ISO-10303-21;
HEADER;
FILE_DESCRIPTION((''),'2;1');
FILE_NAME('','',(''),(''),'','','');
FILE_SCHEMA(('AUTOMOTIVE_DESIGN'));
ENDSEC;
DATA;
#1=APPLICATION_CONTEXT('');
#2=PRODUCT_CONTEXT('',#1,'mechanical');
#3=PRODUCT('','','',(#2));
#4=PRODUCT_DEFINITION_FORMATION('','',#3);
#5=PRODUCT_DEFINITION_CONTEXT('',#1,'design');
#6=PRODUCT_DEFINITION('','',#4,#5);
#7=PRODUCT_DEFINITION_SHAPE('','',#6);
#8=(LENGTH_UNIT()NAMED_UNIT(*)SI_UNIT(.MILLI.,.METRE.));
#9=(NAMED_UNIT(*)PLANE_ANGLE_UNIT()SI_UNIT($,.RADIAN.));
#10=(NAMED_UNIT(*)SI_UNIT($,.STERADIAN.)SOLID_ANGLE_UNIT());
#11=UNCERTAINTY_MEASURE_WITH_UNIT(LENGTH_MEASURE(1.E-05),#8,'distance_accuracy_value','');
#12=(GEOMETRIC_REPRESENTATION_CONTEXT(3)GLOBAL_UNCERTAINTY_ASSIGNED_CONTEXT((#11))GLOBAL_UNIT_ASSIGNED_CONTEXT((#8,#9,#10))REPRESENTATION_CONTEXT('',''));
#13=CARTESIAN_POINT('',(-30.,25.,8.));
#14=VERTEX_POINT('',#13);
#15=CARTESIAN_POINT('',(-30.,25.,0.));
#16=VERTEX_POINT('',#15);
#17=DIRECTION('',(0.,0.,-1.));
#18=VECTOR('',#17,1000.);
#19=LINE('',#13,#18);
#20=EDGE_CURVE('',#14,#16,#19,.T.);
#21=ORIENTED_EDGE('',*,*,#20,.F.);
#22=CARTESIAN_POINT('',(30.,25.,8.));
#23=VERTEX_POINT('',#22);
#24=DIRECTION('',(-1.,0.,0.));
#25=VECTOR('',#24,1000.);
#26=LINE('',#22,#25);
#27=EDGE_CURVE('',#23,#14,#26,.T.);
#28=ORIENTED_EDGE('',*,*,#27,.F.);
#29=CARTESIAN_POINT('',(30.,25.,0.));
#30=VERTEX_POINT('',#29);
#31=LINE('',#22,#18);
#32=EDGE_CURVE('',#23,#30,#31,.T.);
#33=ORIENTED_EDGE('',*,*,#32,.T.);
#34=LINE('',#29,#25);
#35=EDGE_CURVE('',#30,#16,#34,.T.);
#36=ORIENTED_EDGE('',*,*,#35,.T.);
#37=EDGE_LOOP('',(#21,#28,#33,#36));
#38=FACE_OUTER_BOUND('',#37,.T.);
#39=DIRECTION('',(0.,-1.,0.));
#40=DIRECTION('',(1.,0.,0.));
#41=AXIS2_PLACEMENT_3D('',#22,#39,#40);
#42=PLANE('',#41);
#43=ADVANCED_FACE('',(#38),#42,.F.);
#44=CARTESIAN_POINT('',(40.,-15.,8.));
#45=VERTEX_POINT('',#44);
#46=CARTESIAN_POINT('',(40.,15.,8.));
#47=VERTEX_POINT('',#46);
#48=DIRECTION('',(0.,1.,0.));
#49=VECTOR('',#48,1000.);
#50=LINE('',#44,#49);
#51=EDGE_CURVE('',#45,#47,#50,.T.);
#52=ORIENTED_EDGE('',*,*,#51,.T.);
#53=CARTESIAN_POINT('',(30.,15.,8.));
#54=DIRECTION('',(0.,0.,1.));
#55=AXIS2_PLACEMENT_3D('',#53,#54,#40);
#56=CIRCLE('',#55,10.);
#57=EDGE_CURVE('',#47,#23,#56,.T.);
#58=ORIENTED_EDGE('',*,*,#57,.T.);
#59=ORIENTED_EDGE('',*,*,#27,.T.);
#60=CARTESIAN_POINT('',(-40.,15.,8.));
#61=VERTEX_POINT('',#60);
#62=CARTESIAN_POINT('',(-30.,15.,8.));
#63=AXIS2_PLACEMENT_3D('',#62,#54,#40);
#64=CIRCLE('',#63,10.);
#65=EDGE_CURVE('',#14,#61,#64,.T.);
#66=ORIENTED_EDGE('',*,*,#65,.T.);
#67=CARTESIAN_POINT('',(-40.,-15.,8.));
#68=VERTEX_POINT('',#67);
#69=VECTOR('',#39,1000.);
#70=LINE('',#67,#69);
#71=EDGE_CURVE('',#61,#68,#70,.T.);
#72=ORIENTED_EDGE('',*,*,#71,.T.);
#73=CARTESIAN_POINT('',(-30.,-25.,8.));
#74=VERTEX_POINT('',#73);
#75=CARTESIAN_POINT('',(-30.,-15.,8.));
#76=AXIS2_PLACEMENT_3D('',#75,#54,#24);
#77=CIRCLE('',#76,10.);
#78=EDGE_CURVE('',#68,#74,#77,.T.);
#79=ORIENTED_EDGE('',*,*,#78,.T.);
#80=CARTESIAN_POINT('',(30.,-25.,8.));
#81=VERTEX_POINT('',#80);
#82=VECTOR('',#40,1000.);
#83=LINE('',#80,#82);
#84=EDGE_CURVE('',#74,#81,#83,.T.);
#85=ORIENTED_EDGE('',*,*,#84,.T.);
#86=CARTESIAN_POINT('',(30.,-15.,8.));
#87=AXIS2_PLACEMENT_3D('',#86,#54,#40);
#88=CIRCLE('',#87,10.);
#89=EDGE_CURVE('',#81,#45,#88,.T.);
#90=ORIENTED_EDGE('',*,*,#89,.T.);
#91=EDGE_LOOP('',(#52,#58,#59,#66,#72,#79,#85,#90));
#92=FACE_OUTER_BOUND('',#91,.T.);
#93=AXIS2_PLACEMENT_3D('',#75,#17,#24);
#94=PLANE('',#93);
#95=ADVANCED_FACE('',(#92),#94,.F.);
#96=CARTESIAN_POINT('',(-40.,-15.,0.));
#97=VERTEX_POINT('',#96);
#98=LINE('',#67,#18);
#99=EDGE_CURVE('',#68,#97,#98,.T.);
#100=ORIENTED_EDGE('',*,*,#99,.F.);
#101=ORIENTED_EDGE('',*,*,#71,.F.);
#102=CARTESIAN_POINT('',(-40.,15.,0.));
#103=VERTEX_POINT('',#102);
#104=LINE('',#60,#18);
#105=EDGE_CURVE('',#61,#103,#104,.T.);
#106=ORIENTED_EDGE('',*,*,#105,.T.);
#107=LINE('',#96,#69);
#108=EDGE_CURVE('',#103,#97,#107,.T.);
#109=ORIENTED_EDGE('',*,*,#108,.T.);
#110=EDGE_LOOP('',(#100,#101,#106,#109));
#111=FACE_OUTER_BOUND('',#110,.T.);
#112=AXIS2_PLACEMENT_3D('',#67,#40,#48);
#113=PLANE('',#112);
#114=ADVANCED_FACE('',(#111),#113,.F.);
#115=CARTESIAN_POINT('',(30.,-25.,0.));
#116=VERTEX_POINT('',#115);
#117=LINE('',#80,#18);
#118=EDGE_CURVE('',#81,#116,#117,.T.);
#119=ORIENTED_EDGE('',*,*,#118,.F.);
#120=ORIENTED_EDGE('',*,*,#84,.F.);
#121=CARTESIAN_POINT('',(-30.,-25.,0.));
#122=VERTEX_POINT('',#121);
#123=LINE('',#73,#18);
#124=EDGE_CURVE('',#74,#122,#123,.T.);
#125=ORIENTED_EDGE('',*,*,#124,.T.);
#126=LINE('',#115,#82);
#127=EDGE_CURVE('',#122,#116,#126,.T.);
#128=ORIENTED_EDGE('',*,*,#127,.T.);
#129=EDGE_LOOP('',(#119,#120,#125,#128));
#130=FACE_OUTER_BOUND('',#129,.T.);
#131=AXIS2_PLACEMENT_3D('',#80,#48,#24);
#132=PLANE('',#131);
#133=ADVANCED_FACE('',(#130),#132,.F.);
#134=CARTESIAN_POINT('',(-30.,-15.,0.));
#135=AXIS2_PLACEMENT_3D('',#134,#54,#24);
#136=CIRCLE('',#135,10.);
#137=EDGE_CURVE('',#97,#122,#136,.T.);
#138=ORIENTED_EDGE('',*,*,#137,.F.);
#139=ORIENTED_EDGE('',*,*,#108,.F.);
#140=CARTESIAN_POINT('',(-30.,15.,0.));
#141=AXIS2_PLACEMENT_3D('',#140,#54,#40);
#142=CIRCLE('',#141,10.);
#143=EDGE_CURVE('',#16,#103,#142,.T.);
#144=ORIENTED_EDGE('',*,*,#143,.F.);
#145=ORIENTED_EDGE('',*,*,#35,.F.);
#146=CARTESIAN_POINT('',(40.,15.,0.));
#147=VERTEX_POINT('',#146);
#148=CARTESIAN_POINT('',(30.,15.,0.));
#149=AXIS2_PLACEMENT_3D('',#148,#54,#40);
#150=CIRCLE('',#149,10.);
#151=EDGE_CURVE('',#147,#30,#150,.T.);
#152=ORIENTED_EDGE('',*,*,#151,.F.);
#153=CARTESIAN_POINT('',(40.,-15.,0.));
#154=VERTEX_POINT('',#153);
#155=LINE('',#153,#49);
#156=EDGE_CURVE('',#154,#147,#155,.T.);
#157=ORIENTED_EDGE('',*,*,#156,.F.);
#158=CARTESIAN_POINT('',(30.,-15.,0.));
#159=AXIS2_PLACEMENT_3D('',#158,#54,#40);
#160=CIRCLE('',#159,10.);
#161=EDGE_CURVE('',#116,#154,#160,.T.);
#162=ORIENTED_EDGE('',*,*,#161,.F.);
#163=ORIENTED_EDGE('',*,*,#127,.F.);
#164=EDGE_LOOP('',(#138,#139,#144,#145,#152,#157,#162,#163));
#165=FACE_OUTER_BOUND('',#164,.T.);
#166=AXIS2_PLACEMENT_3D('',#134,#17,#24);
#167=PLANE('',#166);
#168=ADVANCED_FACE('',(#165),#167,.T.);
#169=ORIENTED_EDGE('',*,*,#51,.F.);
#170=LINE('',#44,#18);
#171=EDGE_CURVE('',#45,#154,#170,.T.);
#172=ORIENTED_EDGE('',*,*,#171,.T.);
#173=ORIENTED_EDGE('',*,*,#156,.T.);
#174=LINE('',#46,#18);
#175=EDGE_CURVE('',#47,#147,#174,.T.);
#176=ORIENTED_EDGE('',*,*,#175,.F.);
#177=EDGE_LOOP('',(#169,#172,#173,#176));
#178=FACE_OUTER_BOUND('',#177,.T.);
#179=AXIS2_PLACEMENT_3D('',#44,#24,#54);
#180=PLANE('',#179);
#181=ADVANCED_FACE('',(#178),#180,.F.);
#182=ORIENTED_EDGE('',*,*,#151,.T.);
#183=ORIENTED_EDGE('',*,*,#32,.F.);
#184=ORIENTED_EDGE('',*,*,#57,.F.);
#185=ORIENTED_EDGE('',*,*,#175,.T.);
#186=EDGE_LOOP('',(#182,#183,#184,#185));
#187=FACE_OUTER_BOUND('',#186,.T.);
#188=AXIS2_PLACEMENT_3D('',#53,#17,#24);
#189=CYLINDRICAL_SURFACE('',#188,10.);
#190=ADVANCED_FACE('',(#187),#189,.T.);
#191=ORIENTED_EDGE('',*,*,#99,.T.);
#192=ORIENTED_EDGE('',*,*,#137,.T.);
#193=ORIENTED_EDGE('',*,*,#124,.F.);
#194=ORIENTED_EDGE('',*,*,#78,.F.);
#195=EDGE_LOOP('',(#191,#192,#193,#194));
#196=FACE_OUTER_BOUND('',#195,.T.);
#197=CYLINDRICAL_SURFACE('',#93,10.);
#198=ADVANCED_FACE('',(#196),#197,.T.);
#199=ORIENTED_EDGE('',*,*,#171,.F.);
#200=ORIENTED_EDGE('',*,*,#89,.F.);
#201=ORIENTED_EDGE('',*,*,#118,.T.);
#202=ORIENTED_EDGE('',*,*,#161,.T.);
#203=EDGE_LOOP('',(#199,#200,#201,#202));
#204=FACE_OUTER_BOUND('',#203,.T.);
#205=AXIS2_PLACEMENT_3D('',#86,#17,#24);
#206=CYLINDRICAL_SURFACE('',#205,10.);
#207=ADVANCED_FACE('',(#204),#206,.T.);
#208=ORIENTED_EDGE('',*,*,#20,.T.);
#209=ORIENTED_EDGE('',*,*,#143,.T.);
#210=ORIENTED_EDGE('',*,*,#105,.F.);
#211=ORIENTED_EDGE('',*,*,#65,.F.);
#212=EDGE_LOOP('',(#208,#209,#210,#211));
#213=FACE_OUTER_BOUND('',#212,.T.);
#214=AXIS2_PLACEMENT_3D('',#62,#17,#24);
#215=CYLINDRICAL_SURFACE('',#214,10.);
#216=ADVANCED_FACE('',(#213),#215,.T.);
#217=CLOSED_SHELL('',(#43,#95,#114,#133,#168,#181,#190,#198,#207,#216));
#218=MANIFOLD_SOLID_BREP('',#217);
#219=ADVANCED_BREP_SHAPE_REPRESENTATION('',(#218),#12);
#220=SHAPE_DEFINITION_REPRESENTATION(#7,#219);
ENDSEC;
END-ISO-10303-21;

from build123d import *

# Parameters (mm, degrees)
BOSS_EXTRUDE1_DEPTH = 8


with BuildPart() as part:
    # Sketch1 → Boss-Extrude1 (new body)
    with BuildSketch(Plane.XY):
        with BuildLine():
            Line((30, -25), (-30, -25))
            ThreePointArc((-30, -25), (-37.071067812, -22.071067812), (-40, -15))
            Line((-40, -15), (-40, 15))
            ThreePointArc((-40, 15), (-37.071067812, 22.071067812), (-30, 25))
            Line((-30, 25), (30, 25))
            ThreePointArc((30, 25), (37.071067812, 22.071067812), (40, 15))
            Line((40, 15), (40, -15))
            ThreePointArc((40, -15), (37.071067812, -22.071067812), (30, -25))
        make_face()
    extrude(amount=BOSS_EXTRUDE1_DEPTH)


solid = part.part
